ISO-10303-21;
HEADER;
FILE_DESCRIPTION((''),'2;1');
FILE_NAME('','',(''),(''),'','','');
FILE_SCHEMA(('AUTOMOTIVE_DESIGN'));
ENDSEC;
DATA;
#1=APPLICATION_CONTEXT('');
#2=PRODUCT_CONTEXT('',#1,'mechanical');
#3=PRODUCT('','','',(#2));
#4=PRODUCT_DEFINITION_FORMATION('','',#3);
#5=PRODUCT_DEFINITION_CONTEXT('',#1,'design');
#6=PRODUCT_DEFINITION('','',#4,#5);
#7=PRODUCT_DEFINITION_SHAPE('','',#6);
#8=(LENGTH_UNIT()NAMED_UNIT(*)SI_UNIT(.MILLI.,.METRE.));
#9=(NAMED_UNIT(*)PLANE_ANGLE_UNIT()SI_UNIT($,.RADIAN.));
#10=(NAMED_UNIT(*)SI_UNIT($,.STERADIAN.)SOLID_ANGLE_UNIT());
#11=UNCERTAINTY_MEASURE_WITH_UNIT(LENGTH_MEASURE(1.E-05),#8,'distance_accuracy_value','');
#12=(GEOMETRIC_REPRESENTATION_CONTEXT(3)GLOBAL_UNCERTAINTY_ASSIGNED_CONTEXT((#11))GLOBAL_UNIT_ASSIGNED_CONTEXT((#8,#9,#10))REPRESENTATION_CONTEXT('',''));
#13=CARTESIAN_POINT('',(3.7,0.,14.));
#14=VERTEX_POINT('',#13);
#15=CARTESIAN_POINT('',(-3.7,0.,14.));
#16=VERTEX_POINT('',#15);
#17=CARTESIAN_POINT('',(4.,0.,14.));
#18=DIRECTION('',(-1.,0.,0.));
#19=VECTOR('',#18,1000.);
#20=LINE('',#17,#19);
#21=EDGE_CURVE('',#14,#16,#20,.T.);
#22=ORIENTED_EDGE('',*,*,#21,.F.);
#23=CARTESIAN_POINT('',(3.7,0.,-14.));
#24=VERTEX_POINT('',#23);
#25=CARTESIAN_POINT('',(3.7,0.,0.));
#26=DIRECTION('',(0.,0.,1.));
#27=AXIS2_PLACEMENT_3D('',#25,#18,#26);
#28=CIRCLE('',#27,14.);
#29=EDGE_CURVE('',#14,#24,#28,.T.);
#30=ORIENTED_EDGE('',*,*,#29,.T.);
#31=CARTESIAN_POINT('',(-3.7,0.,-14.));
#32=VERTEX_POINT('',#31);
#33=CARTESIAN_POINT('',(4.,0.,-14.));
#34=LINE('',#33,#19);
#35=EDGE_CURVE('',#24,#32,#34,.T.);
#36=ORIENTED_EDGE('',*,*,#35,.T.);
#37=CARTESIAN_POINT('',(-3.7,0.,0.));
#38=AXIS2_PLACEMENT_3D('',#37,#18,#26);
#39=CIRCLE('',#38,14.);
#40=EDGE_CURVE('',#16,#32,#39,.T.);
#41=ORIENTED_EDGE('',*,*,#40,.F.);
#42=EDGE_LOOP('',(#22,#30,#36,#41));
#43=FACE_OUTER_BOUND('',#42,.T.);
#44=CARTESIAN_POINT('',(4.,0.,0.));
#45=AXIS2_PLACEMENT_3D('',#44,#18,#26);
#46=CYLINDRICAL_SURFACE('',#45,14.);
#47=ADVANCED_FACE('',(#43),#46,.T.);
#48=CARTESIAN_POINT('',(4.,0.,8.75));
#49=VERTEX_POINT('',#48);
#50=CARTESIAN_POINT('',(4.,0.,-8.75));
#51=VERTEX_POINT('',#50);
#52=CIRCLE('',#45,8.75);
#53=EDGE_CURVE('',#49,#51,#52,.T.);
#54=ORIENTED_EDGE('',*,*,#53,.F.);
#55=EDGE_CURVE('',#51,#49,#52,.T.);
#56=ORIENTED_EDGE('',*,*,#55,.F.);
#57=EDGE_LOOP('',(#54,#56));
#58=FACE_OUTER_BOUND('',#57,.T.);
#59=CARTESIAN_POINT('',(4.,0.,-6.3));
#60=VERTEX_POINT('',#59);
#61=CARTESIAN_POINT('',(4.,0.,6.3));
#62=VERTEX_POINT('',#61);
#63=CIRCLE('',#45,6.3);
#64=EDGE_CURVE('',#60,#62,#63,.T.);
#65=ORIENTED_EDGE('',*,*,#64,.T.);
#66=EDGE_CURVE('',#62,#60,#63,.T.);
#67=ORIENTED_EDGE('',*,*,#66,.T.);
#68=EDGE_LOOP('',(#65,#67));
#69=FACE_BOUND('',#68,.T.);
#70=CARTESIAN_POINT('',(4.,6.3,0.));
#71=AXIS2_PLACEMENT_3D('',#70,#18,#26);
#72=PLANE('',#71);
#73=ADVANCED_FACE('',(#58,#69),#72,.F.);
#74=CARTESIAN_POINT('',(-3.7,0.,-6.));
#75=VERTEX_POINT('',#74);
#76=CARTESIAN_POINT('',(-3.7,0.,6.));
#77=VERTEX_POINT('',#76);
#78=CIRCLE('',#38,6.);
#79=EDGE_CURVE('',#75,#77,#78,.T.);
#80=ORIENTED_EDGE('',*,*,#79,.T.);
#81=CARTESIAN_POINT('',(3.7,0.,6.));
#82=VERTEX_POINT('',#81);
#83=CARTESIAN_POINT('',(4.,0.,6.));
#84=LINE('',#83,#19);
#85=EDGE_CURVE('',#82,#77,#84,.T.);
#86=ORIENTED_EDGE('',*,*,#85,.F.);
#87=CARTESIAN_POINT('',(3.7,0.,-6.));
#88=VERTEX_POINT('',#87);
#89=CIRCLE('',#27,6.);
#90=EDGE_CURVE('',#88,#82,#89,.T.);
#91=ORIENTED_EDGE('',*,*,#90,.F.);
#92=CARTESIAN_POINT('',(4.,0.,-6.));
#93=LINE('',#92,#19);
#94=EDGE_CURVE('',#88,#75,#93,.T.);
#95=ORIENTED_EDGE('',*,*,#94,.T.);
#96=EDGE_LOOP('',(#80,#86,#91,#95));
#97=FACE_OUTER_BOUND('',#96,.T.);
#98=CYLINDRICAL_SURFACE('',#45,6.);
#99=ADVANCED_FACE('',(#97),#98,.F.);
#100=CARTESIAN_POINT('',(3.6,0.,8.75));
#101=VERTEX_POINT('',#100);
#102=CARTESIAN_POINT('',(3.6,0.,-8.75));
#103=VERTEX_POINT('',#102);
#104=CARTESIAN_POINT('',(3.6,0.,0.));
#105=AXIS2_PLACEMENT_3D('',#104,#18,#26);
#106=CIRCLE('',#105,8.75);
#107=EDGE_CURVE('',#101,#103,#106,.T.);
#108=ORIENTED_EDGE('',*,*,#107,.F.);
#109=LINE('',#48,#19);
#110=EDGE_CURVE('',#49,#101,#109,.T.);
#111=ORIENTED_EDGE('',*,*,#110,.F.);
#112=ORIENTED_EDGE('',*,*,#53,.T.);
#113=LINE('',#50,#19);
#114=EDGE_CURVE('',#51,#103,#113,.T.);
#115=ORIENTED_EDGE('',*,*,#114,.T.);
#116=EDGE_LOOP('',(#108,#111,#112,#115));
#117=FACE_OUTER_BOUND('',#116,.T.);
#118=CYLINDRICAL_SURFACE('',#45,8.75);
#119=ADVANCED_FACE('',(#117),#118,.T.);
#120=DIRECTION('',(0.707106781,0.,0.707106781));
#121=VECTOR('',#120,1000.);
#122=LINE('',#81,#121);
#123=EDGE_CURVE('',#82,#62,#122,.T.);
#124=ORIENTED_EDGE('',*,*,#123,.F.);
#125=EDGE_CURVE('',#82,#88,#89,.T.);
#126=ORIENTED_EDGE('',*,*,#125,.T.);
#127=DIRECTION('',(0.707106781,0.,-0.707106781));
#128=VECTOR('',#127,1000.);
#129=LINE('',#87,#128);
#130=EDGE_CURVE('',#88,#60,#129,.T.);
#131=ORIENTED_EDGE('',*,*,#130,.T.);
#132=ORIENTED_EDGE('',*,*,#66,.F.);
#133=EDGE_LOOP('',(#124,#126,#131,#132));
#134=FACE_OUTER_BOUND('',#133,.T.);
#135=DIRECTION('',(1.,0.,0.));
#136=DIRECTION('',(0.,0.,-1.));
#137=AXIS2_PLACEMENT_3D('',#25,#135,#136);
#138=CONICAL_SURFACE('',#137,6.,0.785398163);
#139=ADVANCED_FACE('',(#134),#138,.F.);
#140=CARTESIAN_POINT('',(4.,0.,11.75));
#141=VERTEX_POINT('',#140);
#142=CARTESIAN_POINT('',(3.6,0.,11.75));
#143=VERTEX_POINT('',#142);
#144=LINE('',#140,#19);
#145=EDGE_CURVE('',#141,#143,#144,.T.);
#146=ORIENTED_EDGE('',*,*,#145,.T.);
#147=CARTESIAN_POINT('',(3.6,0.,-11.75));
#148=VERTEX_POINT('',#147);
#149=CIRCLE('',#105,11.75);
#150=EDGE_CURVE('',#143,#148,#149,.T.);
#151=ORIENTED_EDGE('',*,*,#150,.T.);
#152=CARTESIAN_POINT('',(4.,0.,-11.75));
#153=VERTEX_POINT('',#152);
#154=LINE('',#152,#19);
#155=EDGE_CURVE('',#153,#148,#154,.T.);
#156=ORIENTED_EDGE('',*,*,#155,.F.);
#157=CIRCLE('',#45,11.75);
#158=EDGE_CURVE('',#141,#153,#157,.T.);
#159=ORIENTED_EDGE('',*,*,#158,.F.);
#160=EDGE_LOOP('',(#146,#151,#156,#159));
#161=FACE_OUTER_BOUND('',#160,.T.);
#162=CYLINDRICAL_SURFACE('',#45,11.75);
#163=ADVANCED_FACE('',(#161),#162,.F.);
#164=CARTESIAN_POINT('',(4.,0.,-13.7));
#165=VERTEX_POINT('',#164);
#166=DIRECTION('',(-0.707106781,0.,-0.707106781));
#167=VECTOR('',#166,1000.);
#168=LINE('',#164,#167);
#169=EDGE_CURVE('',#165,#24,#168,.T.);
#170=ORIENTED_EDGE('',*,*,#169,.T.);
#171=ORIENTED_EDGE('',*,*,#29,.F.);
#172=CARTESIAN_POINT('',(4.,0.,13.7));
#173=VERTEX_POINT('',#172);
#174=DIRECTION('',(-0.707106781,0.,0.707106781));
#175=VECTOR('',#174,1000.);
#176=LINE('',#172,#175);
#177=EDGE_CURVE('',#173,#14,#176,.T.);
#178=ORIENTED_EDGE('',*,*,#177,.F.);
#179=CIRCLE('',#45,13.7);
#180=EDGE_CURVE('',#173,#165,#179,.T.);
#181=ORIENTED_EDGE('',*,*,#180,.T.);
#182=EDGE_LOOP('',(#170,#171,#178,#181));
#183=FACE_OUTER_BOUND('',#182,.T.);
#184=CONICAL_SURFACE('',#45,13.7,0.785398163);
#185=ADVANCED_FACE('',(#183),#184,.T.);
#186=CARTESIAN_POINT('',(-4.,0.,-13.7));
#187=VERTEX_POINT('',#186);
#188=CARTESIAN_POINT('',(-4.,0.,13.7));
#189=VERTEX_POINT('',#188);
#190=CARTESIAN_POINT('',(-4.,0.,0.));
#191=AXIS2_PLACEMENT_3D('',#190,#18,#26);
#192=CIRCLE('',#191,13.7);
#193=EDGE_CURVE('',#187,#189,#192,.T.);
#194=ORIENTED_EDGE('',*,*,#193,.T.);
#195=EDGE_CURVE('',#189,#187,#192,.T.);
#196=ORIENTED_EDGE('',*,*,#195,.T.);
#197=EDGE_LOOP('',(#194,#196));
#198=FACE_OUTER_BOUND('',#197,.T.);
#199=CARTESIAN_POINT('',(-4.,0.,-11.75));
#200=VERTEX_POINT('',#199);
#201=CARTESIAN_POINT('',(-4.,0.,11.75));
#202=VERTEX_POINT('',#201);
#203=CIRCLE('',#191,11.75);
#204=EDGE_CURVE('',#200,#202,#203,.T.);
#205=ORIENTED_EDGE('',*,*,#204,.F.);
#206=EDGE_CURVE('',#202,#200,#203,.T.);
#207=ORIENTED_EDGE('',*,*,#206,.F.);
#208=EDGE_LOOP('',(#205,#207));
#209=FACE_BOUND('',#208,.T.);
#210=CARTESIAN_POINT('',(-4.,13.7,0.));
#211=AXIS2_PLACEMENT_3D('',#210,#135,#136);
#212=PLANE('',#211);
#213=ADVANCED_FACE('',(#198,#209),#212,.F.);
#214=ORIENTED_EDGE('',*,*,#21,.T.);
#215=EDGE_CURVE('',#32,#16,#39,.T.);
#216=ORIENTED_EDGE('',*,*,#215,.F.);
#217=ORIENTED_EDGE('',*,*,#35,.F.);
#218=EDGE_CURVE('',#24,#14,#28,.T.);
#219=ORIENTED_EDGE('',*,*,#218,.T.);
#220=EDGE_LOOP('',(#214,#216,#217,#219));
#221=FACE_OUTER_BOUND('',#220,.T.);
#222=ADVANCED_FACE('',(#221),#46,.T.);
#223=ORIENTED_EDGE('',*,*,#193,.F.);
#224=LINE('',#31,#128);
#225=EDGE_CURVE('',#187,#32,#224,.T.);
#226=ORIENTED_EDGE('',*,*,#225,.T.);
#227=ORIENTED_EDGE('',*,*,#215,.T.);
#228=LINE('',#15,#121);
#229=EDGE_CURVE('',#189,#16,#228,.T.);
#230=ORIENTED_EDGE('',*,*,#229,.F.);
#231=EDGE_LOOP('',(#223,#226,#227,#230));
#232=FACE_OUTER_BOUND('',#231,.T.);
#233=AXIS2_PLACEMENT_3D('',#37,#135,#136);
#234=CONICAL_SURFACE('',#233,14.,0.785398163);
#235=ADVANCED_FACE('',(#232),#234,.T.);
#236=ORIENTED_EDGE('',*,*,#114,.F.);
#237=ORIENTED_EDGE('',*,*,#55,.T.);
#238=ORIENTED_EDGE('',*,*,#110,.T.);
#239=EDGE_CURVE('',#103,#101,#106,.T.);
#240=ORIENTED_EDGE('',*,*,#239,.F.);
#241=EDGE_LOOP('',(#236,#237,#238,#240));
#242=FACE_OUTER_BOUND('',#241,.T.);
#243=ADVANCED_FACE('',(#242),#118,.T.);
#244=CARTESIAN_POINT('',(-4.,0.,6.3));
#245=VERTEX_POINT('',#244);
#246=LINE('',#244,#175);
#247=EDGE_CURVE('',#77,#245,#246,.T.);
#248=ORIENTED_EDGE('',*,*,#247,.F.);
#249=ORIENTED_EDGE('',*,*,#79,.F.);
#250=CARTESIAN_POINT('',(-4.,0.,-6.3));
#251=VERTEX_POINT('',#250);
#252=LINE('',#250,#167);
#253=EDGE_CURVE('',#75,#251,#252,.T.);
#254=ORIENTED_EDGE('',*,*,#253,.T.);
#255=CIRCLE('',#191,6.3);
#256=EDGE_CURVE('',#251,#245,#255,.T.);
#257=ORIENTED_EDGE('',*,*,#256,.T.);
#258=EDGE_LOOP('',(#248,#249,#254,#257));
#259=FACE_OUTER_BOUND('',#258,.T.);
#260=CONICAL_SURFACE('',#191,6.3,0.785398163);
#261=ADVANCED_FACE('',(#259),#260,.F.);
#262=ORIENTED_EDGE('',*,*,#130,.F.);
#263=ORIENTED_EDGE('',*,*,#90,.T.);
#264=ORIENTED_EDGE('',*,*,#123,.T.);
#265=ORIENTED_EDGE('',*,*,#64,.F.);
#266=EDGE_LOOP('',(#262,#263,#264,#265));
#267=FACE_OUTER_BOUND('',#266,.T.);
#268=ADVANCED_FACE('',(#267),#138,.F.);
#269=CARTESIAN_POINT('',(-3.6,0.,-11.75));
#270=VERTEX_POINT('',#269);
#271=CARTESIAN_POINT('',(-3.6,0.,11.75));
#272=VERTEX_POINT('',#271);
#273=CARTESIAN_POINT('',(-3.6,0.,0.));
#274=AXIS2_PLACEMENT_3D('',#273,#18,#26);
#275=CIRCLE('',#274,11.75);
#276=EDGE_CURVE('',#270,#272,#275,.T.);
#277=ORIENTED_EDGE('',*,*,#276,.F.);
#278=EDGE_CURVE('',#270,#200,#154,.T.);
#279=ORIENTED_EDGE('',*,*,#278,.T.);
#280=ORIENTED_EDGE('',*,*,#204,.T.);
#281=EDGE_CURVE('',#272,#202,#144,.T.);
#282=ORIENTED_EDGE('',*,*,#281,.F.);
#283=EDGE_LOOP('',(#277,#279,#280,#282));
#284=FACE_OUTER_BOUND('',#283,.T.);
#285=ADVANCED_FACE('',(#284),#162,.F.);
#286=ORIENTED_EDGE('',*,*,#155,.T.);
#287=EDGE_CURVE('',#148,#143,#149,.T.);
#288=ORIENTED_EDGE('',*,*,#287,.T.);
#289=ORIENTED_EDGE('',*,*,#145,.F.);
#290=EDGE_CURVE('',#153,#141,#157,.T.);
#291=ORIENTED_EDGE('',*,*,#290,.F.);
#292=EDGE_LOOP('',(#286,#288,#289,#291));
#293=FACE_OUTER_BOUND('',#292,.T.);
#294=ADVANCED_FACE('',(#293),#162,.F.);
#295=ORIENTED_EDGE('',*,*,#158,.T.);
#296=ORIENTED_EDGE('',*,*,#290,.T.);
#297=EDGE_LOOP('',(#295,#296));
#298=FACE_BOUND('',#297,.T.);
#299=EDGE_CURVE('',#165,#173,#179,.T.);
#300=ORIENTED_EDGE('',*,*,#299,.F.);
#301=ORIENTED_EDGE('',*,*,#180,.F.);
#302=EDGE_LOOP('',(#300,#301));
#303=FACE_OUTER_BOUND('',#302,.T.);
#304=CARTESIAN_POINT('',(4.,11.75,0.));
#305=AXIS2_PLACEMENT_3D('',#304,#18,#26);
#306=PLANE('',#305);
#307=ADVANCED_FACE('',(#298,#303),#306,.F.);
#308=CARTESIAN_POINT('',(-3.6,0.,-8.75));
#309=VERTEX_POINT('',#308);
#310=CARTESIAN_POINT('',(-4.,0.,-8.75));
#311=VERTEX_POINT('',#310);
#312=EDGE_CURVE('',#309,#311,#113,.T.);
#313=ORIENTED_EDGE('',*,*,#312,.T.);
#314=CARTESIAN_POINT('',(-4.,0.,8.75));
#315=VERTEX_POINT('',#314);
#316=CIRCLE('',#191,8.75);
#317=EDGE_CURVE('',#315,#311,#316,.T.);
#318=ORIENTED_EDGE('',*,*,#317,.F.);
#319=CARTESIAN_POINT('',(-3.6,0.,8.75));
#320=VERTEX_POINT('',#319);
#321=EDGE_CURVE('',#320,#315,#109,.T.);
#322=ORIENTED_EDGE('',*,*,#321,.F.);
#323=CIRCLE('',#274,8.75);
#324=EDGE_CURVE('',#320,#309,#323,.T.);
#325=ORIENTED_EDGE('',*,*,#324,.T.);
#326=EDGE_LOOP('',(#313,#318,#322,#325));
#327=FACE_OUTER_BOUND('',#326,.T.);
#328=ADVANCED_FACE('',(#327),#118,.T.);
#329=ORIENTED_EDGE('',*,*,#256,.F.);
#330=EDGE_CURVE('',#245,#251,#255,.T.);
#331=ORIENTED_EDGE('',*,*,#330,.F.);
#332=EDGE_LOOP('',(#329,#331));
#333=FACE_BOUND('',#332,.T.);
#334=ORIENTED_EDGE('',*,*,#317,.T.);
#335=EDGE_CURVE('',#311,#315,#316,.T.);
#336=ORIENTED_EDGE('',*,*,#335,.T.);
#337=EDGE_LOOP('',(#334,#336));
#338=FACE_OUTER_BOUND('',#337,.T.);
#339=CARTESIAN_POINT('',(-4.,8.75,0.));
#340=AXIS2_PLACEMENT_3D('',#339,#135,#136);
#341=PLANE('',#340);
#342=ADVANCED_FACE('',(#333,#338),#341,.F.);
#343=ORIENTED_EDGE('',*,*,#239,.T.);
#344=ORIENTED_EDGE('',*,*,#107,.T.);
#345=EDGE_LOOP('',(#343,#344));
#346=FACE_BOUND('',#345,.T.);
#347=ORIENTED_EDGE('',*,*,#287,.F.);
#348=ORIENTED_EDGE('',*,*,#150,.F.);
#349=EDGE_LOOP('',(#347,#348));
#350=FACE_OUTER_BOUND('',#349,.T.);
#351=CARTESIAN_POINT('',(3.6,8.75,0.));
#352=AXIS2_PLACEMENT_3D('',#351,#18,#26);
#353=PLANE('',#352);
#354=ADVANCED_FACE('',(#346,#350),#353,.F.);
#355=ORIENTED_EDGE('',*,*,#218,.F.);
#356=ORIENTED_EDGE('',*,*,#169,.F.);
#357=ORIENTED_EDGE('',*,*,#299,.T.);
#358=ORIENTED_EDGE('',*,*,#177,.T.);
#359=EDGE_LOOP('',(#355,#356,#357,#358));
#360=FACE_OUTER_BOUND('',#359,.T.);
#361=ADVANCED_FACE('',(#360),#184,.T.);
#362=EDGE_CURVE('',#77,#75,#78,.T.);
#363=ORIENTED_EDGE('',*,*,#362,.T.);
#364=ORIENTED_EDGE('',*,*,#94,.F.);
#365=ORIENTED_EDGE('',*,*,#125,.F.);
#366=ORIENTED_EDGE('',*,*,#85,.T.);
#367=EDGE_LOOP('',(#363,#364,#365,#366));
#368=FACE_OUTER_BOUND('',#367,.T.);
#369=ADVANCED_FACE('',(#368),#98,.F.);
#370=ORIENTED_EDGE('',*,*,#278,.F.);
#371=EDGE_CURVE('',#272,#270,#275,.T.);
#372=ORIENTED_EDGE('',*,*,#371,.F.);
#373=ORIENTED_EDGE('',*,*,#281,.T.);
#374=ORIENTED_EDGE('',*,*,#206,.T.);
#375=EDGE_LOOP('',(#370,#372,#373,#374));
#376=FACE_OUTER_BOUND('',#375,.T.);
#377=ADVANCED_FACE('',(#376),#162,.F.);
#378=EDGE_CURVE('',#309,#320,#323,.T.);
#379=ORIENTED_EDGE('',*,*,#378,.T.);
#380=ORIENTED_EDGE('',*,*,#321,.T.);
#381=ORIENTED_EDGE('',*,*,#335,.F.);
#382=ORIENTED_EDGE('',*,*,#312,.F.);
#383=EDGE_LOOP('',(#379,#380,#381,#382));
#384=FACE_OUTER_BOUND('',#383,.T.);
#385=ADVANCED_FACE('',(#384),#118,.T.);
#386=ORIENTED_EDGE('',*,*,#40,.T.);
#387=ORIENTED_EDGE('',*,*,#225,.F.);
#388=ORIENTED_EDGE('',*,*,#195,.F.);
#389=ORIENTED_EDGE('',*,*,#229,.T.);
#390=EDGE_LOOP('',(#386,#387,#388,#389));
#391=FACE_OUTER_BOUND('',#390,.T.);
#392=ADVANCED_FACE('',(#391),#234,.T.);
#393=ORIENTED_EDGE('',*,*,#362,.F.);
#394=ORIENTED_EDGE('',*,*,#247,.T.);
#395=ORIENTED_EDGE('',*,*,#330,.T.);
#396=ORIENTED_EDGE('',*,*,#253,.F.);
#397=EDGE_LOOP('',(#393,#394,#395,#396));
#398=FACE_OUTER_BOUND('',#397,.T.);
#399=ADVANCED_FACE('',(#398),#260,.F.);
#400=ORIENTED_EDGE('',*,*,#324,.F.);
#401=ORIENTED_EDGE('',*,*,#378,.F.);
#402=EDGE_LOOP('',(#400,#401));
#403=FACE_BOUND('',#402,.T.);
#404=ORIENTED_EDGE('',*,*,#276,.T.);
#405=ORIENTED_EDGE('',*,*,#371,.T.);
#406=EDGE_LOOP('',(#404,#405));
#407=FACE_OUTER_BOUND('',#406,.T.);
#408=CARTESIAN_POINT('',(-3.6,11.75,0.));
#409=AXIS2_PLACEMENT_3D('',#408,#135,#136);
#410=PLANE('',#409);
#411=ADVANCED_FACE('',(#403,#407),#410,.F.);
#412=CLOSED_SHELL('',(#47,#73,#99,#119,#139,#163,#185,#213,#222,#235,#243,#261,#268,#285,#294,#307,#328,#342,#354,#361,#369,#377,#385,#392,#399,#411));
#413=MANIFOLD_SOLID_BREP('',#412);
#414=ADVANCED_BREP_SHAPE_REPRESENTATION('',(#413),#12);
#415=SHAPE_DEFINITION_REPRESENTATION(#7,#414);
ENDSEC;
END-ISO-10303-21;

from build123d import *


with BuildPart() as part:
    # 草图1 → 旋转1 (revolve)
    with BuildSketch(Plane.XY, mode=Mode.PRIVATE) as revolve_1_sk:
        Polygon((-4, 13.7), (-4, 11.75), (-3.6, 11.75), (-3.6, 8.75), (-4, 8.75), (-4, 6.3), (-3.7, 6), (3.7, 6), (4, 6.3), (4, 8.75), (3.6, 8.75), (3.6, 11.75), (4, 11.75), (4, 13.7), (3.7, 14), (-3.7, 14), align=None)
    revolve(revolve_1_sk.sketch.rotate(Axis((4, 0, 0), (-1, 0, 0)), 270), axis=Axis((4, 0, 0), (-1, 0, 0)))


solid = part.part
